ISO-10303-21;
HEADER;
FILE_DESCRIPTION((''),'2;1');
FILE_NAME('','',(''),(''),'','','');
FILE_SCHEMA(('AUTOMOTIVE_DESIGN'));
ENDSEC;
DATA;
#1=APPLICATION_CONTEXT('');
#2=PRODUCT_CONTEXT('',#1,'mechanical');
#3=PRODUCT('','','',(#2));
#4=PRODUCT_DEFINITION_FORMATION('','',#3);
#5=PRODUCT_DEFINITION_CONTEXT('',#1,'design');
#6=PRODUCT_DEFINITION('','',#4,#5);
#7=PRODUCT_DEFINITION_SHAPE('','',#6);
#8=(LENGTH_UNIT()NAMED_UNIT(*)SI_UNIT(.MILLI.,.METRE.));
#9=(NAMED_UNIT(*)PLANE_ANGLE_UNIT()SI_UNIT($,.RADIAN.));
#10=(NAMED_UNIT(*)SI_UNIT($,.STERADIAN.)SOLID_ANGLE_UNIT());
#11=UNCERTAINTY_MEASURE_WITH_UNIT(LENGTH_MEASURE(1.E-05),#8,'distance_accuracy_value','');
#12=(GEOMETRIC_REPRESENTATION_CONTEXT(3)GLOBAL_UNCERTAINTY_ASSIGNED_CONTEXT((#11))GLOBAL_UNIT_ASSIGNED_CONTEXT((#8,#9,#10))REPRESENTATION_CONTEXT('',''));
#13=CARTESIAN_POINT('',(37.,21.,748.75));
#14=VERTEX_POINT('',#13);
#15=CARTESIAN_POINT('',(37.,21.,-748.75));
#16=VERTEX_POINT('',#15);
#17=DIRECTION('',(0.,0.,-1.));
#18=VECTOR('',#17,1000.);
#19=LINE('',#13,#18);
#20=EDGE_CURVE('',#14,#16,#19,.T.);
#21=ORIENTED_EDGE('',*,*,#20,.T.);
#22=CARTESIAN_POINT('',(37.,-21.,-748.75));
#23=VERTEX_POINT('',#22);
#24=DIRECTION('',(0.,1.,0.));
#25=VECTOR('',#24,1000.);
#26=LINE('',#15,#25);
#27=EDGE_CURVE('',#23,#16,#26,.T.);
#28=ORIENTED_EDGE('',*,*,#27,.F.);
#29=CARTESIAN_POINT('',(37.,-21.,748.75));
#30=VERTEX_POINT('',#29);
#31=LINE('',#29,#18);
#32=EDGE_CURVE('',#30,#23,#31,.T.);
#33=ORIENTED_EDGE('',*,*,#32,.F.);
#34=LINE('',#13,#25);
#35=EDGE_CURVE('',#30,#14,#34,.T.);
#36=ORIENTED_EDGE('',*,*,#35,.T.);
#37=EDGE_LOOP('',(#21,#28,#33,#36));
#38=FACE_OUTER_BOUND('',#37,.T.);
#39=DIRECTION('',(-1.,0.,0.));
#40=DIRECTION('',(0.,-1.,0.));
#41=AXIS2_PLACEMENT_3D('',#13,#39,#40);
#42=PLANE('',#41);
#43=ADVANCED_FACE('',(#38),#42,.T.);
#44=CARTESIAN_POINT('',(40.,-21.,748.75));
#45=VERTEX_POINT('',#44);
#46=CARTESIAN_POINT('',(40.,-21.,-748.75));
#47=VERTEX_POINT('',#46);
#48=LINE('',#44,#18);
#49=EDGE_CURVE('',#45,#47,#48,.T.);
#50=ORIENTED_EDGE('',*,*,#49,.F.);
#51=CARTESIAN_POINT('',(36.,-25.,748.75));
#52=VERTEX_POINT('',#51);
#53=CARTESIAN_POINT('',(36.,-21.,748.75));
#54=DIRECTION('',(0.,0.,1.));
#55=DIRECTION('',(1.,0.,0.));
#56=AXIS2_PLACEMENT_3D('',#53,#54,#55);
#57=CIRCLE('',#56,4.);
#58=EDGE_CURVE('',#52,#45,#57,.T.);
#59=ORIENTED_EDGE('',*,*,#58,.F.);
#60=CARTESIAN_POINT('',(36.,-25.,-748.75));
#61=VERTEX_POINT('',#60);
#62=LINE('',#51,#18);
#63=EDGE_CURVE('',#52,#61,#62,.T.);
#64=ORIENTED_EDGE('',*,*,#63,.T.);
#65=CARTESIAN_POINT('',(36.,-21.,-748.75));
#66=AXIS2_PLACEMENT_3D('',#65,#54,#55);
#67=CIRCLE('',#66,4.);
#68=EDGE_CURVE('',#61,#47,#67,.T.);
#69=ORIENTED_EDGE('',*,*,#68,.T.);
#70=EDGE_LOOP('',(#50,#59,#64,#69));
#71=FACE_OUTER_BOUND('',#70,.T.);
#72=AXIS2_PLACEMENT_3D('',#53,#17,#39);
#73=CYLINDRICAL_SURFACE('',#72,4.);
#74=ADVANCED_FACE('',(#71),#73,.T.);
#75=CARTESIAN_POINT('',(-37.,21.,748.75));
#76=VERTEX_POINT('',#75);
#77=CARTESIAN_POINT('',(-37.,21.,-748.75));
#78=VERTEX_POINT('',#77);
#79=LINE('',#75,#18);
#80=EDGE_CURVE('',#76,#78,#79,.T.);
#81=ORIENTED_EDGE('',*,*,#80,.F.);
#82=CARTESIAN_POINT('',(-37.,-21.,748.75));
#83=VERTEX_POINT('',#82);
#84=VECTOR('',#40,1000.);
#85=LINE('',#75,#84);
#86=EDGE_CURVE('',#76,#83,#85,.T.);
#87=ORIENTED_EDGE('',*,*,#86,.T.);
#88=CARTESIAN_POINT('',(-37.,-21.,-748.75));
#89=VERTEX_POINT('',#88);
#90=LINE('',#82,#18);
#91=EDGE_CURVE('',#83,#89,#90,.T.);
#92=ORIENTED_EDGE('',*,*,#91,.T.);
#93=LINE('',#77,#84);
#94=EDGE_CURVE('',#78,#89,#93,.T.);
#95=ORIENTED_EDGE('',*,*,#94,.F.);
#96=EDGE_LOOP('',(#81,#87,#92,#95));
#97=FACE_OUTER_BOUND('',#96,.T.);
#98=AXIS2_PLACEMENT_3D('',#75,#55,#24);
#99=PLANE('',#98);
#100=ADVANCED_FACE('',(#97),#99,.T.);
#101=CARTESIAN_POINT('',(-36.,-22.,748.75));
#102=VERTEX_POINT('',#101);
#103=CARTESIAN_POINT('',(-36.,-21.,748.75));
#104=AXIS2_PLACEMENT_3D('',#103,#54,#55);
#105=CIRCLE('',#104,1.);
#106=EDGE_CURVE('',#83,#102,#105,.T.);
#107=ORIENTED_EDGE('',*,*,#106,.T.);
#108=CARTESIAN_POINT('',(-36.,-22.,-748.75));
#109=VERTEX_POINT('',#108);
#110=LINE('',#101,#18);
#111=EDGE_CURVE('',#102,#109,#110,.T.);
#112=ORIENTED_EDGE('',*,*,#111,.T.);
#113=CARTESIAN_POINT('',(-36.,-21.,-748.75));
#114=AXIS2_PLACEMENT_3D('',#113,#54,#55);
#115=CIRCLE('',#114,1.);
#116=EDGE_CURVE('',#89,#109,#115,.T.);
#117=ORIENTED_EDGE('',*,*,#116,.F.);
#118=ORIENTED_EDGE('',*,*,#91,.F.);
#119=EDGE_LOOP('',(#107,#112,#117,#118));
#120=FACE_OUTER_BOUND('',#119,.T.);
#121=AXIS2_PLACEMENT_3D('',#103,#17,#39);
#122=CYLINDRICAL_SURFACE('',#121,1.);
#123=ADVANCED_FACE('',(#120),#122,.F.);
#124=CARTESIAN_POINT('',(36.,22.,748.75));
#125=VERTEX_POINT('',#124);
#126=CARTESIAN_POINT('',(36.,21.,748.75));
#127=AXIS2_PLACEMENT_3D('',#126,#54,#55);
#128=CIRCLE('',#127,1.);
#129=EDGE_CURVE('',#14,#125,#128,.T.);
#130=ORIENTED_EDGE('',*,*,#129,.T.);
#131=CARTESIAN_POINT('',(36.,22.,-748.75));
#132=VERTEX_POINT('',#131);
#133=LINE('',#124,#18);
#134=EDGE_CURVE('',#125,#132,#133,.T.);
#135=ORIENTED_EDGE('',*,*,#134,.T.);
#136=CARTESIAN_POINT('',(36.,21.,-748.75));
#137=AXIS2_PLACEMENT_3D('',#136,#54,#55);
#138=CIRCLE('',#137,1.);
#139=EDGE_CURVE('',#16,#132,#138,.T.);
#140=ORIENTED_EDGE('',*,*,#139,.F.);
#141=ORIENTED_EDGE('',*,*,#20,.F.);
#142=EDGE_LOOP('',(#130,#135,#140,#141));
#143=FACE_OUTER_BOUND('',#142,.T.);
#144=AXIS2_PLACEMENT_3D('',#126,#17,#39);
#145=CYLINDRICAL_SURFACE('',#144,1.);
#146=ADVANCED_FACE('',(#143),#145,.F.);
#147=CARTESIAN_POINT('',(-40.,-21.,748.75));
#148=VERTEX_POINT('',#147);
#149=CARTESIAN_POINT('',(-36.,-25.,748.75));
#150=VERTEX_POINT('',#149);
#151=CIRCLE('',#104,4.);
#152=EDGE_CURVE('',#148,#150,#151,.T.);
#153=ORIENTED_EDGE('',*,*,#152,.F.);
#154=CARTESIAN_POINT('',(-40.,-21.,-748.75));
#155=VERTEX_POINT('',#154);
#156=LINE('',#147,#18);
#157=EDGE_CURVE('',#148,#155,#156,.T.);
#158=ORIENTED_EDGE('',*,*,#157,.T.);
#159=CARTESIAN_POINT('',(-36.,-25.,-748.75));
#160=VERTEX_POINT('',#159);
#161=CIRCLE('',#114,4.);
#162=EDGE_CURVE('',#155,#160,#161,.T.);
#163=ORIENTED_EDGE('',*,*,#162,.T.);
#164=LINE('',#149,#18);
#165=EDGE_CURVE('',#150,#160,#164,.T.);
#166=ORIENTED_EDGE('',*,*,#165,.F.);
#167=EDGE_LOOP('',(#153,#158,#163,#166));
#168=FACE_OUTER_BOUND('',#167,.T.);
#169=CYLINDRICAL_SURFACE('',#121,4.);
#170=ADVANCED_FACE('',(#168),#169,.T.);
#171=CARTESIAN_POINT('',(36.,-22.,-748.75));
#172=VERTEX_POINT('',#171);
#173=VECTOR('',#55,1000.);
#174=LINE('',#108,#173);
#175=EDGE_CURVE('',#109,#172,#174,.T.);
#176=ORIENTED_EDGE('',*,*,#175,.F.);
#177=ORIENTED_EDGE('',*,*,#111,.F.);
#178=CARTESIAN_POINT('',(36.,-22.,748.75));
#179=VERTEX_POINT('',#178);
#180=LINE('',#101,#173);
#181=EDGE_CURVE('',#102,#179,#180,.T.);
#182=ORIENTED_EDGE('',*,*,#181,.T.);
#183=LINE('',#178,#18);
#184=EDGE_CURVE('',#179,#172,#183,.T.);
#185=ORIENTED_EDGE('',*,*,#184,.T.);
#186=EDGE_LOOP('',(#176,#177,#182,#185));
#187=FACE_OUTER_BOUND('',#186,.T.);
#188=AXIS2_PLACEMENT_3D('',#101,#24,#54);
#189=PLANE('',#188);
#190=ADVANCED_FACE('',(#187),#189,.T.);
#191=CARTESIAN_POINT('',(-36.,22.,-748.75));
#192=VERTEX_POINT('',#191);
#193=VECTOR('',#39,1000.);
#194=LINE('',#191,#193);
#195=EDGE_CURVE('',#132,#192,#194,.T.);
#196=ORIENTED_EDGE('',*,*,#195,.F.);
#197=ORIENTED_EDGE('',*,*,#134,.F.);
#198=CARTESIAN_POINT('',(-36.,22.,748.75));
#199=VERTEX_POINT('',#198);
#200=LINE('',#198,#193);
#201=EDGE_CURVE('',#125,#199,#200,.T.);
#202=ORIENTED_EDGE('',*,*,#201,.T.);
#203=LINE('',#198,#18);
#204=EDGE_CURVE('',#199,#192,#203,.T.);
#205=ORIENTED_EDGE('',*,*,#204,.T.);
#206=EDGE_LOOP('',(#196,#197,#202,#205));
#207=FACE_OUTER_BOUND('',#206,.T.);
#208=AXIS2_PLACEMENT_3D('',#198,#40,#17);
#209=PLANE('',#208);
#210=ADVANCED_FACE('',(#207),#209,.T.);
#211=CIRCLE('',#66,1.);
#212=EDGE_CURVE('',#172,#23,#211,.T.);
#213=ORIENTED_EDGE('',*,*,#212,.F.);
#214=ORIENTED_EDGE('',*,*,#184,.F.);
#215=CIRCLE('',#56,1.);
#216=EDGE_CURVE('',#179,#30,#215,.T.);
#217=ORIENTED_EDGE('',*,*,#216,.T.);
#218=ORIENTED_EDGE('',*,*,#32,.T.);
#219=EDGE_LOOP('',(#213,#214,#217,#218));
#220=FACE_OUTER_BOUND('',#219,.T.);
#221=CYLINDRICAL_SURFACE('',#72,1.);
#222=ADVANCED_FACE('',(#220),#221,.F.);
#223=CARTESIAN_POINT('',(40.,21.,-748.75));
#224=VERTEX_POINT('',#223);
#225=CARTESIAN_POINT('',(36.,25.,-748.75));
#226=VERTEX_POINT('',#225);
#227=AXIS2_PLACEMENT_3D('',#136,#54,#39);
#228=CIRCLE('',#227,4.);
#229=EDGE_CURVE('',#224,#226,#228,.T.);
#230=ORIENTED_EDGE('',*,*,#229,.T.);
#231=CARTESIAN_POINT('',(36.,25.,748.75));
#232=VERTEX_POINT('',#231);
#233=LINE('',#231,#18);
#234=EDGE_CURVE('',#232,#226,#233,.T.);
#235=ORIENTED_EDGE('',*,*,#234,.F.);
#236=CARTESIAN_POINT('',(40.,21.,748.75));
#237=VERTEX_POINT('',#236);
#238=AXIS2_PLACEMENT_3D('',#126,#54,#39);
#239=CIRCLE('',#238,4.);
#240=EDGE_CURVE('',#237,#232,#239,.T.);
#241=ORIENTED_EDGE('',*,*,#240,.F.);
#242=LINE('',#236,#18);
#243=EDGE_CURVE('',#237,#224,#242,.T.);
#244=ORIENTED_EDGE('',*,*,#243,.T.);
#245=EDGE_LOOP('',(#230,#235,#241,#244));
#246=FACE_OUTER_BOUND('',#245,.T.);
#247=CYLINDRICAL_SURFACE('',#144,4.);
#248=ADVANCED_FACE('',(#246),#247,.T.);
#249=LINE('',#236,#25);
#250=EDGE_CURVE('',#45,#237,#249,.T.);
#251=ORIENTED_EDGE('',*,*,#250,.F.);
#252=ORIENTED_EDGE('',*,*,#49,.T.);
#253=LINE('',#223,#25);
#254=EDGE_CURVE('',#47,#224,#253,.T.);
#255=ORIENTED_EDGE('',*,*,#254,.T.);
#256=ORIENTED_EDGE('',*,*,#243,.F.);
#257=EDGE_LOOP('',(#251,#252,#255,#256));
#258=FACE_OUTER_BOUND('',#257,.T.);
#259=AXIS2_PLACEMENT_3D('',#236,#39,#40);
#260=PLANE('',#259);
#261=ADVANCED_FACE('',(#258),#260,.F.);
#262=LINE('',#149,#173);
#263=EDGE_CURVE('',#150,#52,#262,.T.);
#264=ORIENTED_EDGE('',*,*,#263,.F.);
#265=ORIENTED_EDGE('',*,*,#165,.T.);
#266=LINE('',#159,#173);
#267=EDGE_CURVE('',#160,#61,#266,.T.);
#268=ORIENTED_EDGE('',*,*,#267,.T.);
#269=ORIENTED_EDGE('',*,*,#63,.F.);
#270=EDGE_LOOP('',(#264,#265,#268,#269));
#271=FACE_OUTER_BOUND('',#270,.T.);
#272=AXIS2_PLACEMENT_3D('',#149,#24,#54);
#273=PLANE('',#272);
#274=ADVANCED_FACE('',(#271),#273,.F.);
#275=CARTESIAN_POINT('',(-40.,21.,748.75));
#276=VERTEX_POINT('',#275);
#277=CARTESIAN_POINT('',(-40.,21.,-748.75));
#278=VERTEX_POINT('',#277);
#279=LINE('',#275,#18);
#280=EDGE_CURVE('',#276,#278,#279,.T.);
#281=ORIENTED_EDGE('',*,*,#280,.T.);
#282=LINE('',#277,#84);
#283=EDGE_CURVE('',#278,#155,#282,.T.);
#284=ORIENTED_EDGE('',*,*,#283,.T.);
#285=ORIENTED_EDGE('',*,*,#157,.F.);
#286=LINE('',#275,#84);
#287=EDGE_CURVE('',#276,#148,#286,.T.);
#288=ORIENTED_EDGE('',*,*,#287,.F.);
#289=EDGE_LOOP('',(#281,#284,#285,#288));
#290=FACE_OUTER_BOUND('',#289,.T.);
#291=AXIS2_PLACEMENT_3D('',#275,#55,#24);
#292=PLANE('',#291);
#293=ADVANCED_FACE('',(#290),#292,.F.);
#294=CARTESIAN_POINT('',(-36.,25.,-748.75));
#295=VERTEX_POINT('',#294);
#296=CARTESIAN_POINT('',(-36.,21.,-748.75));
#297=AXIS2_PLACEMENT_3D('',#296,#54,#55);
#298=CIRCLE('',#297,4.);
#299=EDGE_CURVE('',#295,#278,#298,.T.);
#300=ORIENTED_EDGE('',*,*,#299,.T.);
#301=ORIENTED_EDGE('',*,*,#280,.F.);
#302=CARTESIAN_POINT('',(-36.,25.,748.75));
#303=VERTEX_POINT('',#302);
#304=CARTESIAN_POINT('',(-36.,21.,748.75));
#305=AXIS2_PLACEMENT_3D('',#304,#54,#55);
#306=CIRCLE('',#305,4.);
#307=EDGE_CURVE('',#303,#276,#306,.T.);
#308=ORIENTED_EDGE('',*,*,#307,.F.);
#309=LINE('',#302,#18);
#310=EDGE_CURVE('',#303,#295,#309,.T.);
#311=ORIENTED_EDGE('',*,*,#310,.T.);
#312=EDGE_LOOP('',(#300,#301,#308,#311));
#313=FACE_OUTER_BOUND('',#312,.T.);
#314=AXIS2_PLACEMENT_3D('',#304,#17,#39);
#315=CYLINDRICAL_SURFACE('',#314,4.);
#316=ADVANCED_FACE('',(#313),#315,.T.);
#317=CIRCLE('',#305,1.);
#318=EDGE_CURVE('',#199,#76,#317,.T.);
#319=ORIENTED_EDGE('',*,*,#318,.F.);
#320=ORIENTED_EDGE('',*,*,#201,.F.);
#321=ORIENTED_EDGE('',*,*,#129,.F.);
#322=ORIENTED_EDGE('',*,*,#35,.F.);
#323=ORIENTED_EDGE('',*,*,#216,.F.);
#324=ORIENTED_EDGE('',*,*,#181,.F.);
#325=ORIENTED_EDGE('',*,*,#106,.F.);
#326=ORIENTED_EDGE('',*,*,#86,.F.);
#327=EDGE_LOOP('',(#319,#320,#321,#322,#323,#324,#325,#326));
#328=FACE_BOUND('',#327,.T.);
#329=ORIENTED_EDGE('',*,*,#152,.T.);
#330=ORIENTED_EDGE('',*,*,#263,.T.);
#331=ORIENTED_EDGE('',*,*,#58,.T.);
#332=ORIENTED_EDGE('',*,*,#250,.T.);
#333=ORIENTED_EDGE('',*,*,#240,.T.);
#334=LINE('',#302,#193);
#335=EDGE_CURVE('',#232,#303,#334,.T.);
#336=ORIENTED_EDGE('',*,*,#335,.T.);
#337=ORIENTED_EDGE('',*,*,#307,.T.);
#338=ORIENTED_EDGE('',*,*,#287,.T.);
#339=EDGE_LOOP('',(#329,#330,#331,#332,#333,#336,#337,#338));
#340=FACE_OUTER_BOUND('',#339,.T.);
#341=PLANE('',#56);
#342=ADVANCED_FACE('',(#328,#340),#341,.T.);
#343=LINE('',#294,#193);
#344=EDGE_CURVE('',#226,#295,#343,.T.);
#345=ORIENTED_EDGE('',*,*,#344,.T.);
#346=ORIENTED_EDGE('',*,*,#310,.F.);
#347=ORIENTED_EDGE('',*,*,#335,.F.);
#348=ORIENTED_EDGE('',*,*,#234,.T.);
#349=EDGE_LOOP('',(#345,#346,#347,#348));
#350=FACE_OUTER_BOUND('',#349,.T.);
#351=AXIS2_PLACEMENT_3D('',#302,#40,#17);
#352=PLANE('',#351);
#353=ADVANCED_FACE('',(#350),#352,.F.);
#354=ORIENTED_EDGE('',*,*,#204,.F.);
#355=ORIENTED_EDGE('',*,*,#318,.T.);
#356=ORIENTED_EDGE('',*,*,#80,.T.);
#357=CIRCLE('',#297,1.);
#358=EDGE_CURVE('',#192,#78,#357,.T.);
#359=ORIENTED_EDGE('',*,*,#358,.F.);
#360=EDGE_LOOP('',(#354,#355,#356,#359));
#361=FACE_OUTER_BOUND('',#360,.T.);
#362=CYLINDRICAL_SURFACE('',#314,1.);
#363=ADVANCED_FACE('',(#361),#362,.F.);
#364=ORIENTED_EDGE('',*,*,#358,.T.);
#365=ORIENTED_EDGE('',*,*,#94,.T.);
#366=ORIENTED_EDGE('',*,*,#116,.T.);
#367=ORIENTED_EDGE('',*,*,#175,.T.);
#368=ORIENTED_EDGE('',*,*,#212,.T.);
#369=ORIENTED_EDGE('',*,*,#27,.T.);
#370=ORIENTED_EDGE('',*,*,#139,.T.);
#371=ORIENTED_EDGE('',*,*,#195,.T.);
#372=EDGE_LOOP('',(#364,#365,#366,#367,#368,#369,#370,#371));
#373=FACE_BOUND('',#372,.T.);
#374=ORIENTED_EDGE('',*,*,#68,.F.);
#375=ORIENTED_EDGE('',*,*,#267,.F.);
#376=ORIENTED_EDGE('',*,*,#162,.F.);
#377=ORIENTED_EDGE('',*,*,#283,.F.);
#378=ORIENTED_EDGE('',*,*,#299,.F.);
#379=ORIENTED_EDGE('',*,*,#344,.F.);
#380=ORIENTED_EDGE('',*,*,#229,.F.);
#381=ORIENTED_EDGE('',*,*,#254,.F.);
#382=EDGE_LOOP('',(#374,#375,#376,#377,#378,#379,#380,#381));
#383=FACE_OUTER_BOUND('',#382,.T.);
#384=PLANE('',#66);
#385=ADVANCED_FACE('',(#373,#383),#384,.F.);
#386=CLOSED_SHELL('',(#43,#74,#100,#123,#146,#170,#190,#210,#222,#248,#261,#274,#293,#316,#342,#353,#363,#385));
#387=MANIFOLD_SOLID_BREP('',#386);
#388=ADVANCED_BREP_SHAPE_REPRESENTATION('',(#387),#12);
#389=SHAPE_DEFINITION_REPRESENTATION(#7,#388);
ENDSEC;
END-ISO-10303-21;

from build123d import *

# Parameters (mm, degrees)
EXTRUDE_1_DEPTH = 748.75


with BuildPart() as part:
    # 草图1 → 拉伸-薄壁1 (new, symmetric)
    with BuildSketch(Plane.XY):
        with BuildLine():
            Line((-36, 25), (36, 25))
            ThreePointArc((36, 25), (38.828427125, 23.828427125), (40, 21))
            Line((40, 21), (40, -21))
            ThreePointArc((40, -21), (38.828427125, -23.828427125), (36, -25))
            Line((36, -25), (-36, -25))
            ThreePointArc((-36, -25), (-38.828427125, -23.828427125), (-40, -21))
            Line((-40, -21), (-40, 21))
            ThreePointArc((-40, 21), (-38.828427125, 23.828427125), (-36, 25))
        make_face()
        with BuildLine():
            Line((-36, 22), (36, 22))
            ThreePointArc((36, 22), (36.707106781, 21.707106781), (37, 21))
            Line((37, 21), (37, -21))
            ThreePointArc((37, -21), (36.707106781, -21.707106781), (36, -22))
            Line((36, -22), (-36, -22))
            ThreePointArc((-36, -22), (-36.707106781, -21.707106781), (-37, -21))
            Line((-37, -21), (-37, 21))
            ThreePointArc((-37, 21), (-36.707106781, 21.707106781), (-36, 22))
        make_face(mode=Mode.SUBTRACT)
    extrude(amount=EXTRUDE_1_DEPTH, both=True)


solid = part.part
